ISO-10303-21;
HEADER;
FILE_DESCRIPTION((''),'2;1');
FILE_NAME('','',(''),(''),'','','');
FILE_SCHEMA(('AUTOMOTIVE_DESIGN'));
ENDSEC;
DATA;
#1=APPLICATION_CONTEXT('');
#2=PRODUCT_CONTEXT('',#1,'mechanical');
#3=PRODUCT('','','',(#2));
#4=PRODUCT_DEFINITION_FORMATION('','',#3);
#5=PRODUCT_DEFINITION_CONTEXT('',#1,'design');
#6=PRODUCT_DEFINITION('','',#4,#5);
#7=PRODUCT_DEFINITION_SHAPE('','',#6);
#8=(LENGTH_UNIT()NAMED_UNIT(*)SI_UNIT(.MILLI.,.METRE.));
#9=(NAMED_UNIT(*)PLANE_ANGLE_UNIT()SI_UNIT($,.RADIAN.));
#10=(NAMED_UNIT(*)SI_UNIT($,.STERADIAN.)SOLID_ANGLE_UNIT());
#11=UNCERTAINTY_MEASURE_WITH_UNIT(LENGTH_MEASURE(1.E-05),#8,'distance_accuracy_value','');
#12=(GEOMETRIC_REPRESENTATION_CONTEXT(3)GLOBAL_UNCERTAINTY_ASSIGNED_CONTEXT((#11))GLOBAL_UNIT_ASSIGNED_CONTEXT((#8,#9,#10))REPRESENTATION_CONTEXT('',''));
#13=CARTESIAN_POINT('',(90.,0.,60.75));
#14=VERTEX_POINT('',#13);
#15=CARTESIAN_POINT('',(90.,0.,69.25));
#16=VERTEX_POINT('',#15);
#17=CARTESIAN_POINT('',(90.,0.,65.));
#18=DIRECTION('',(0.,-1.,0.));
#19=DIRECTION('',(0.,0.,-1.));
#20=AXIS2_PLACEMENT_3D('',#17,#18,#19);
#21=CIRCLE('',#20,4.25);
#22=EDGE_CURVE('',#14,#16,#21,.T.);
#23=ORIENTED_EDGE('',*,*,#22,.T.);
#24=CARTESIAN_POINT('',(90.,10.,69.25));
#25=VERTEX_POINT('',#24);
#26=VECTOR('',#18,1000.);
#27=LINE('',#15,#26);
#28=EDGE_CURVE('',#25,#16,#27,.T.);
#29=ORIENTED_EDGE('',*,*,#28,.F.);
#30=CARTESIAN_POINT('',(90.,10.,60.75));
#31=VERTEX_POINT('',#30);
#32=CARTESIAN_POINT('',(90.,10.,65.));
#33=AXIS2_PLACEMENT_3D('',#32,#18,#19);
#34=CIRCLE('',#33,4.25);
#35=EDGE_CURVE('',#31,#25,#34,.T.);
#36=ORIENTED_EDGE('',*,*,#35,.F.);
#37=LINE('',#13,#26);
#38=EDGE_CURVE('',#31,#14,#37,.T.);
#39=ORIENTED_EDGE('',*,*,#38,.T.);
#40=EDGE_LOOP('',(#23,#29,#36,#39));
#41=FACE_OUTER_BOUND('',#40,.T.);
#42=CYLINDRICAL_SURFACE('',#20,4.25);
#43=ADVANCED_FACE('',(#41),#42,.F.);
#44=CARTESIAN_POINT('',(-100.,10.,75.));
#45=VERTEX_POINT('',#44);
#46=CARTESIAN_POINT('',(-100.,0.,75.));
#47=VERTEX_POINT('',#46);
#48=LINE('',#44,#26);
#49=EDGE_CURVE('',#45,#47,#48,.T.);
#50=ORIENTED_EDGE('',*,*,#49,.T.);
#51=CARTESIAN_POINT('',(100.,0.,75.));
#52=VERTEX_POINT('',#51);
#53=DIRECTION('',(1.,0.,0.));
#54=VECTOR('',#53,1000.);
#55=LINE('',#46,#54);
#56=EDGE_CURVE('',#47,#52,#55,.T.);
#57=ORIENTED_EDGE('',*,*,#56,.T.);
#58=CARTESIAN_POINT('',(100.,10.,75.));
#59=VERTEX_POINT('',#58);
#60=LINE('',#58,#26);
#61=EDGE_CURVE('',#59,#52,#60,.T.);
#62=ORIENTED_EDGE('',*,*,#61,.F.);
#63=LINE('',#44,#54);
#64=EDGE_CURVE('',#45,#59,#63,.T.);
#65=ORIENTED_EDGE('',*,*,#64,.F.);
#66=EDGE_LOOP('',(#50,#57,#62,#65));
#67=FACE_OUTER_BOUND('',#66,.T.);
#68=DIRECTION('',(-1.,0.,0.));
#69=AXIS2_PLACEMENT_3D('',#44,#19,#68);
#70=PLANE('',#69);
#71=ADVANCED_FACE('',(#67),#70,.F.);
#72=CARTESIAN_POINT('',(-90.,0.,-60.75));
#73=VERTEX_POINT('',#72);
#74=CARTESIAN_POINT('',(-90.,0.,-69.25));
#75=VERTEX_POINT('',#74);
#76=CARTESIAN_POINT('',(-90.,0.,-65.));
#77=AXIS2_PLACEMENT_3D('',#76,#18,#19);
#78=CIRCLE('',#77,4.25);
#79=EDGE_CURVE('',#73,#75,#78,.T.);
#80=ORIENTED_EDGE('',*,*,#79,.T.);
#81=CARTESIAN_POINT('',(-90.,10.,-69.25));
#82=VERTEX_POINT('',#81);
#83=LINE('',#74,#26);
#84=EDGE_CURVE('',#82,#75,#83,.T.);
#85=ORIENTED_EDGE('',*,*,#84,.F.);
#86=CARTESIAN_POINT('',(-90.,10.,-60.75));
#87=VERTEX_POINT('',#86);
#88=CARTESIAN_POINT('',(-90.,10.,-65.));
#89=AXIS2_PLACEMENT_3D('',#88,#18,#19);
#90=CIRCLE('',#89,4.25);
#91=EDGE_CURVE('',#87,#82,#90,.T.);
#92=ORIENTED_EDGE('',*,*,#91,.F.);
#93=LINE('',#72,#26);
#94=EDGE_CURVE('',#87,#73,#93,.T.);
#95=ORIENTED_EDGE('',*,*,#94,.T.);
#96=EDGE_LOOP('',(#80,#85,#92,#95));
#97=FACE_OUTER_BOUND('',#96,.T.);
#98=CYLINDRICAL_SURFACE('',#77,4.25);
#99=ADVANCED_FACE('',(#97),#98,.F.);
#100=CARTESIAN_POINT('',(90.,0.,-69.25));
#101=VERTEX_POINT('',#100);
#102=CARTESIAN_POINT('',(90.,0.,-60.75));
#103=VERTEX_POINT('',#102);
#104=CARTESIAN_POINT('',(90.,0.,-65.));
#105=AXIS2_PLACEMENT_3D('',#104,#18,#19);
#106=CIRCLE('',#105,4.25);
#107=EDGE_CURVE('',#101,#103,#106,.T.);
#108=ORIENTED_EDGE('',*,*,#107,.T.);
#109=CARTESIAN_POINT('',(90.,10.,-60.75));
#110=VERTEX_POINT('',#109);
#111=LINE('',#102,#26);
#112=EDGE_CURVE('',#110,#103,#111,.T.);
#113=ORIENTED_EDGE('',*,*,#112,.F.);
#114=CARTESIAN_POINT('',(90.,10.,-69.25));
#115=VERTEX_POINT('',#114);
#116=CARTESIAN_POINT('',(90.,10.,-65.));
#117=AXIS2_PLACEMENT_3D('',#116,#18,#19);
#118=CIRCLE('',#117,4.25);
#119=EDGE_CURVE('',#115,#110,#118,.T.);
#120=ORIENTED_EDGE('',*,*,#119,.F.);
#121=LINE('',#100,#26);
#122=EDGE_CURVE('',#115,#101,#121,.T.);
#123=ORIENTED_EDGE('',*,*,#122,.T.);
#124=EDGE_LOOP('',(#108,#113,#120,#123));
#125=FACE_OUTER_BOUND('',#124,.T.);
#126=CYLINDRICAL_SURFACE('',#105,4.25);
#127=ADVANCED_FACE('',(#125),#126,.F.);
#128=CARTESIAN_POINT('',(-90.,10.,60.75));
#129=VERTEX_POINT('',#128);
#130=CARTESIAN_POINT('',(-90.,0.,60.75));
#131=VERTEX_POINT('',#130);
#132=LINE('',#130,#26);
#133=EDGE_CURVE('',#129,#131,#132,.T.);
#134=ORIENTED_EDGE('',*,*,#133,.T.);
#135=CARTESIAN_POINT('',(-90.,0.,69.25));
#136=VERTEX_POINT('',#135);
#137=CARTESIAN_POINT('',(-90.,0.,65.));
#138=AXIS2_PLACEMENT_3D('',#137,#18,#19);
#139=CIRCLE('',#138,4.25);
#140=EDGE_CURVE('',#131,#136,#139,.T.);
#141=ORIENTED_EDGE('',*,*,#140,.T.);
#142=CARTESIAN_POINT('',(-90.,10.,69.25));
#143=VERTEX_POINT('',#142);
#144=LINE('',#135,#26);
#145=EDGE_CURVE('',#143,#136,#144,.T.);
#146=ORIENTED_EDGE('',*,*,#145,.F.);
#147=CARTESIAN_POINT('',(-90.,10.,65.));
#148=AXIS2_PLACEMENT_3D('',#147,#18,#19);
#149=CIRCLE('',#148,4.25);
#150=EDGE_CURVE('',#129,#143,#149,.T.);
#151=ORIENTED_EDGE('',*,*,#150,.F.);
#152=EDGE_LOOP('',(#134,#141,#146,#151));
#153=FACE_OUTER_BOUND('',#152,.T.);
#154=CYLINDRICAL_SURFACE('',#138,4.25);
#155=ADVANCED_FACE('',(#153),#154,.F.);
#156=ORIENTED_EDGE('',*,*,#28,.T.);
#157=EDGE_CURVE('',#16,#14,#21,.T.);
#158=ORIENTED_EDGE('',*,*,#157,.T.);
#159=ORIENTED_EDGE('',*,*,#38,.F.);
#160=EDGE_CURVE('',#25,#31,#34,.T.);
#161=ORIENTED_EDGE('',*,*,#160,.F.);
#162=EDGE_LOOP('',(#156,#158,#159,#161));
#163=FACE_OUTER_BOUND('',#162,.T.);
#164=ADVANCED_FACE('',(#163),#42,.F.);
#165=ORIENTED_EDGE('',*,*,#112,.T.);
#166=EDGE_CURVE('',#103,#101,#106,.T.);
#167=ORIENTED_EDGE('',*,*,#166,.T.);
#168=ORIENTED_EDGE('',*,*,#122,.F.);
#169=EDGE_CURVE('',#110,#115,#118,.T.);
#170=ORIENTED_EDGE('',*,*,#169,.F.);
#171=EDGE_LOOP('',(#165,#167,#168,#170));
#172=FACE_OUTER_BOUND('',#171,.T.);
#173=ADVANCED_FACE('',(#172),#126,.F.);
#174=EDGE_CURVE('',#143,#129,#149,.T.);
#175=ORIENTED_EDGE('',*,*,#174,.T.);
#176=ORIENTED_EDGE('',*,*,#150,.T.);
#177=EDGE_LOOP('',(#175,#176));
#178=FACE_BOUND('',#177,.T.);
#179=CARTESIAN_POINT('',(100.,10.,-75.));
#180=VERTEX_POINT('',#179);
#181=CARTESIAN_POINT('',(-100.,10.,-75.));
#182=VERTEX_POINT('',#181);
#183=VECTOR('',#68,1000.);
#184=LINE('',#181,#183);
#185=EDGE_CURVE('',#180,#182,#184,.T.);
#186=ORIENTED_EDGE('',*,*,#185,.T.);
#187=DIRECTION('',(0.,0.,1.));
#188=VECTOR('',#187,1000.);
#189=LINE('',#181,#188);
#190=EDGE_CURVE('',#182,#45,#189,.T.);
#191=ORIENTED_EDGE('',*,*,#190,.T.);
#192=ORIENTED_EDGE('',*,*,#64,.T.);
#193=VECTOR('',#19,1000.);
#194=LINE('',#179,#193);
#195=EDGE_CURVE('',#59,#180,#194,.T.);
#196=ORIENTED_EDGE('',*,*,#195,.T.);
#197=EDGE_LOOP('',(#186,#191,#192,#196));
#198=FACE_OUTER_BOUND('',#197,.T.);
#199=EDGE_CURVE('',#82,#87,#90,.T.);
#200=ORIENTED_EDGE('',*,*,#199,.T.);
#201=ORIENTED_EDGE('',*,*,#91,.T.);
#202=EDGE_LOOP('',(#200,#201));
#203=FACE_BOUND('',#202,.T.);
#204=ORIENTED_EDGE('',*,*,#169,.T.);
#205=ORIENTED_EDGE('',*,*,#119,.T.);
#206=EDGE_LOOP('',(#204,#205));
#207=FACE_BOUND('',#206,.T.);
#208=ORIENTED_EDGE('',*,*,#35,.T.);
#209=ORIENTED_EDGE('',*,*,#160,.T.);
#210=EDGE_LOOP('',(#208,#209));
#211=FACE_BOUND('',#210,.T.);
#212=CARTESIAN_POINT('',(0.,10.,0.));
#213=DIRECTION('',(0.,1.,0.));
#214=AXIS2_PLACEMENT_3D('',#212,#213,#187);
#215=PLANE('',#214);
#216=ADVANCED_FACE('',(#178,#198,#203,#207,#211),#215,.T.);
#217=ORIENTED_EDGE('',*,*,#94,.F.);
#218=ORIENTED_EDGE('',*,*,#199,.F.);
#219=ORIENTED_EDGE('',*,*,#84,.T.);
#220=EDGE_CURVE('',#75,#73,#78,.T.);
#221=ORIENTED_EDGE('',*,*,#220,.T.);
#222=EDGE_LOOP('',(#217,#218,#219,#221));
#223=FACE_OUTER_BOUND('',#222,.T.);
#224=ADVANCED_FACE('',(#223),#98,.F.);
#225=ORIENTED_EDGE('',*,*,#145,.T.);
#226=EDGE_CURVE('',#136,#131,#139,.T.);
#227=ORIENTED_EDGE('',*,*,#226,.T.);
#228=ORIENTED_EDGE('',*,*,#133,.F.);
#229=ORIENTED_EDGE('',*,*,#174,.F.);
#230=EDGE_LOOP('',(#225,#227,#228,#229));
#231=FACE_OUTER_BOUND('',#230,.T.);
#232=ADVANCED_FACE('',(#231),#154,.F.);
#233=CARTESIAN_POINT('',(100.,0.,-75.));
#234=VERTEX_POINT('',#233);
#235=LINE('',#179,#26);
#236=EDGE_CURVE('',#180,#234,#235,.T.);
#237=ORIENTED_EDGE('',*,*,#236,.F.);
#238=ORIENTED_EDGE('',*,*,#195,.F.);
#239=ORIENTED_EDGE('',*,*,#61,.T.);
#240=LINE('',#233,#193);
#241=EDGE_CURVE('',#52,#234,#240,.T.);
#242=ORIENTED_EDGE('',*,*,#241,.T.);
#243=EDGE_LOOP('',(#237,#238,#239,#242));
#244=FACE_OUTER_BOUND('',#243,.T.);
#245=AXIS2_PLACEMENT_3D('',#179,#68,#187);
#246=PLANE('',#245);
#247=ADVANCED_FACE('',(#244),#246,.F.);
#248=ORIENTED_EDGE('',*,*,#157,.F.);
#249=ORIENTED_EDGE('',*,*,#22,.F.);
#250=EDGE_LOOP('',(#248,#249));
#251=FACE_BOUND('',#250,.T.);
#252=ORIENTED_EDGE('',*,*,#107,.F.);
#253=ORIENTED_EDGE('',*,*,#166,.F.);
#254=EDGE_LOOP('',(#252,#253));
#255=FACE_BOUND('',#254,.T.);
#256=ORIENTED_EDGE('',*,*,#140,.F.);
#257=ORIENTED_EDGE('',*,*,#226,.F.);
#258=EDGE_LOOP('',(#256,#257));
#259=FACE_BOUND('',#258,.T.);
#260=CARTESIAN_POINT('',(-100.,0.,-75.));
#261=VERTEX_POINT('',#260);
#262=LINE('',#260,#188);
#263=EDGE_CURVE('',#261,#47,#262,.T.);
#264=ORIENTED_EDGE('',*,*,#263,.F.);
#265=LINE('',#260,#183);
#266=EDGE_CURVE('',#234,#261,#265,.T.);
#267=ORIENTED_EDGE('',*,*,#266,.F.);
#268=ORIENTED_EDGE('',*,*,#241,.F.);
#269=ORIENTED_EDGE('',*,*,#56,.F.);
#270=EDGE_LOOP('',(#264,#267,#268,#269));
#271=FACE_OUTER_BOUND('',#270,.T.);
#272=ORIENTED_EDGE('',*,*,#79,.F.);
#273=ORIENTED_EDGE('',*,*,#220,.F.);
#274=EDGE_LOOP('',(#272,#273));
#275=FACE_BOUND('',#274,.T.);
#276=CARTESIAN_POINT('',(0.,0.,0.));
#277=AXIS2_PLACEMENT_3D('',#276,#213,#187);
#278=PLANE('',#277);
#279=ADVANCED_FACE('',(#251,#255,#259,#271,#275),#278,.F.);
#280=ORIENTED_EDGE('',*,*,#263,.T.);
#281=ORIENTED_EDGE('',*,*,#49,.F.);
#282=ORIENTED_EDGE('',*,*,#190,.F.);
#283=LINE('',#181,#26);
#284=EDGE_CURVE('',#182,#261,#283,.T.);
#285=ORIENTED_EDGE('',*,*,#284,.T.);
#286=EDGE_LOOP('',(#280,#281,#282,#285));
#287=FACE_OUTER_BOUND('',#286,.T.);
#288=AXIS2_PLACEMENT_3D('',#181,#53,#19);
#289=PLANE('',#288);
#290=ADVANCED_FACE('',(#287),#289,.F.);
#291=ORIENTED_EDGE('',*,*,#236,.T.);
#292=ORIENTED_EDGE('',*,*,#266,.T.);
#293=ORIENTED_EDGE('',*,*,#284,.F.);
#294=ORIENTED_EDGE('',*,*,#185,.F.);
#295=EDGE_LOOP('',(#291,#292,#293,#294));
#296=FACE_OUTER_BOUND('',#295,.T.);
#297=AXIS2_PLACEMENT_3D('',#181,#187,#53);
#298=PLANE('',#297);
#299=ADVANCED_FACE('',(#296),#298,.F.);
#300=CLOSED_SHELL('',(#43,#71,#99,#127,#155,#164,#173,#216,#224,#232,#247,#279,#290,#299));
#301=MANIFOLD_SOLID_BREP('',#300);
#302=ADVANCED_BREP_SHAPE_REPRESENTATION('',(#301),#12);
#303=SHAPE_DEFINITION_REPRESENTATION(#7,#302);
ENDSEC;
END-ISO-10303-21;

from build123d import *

# Parameters (mm, degrees)
SKETCH_1_W          = 200
SKETCH_1_H          = 150
EXTRUDE_1_DEPTH     = 10
HOLE_WIZARD_M10_1_D = 8.5


with BuildPart() as part:
    # 草图1 → 凸台-拉伸1 (new body)
    with BuildSketch(Plane(origin=(0, 0, 0), x_dir=(1, 0, 0), z_dir=(0, 1, 0))):
        Rectangle(SKETCH_1_W, SKETCH_1_H)
    extrude(amount=EXTRUDE_1_DEPTH)

    # M10 螺纹孔1 (through all)
    with Locations(Plane(origin=(0, 0, 0), x_dir=(-1, 0, 0), z_dir=(0, -1, 0))):
        with Locations((90, -65), (90, 65), (-90, 65), (-90, -65)):
            Hole(HOLE_WIZARD_M10_1_D / 2)


solid = part.part
